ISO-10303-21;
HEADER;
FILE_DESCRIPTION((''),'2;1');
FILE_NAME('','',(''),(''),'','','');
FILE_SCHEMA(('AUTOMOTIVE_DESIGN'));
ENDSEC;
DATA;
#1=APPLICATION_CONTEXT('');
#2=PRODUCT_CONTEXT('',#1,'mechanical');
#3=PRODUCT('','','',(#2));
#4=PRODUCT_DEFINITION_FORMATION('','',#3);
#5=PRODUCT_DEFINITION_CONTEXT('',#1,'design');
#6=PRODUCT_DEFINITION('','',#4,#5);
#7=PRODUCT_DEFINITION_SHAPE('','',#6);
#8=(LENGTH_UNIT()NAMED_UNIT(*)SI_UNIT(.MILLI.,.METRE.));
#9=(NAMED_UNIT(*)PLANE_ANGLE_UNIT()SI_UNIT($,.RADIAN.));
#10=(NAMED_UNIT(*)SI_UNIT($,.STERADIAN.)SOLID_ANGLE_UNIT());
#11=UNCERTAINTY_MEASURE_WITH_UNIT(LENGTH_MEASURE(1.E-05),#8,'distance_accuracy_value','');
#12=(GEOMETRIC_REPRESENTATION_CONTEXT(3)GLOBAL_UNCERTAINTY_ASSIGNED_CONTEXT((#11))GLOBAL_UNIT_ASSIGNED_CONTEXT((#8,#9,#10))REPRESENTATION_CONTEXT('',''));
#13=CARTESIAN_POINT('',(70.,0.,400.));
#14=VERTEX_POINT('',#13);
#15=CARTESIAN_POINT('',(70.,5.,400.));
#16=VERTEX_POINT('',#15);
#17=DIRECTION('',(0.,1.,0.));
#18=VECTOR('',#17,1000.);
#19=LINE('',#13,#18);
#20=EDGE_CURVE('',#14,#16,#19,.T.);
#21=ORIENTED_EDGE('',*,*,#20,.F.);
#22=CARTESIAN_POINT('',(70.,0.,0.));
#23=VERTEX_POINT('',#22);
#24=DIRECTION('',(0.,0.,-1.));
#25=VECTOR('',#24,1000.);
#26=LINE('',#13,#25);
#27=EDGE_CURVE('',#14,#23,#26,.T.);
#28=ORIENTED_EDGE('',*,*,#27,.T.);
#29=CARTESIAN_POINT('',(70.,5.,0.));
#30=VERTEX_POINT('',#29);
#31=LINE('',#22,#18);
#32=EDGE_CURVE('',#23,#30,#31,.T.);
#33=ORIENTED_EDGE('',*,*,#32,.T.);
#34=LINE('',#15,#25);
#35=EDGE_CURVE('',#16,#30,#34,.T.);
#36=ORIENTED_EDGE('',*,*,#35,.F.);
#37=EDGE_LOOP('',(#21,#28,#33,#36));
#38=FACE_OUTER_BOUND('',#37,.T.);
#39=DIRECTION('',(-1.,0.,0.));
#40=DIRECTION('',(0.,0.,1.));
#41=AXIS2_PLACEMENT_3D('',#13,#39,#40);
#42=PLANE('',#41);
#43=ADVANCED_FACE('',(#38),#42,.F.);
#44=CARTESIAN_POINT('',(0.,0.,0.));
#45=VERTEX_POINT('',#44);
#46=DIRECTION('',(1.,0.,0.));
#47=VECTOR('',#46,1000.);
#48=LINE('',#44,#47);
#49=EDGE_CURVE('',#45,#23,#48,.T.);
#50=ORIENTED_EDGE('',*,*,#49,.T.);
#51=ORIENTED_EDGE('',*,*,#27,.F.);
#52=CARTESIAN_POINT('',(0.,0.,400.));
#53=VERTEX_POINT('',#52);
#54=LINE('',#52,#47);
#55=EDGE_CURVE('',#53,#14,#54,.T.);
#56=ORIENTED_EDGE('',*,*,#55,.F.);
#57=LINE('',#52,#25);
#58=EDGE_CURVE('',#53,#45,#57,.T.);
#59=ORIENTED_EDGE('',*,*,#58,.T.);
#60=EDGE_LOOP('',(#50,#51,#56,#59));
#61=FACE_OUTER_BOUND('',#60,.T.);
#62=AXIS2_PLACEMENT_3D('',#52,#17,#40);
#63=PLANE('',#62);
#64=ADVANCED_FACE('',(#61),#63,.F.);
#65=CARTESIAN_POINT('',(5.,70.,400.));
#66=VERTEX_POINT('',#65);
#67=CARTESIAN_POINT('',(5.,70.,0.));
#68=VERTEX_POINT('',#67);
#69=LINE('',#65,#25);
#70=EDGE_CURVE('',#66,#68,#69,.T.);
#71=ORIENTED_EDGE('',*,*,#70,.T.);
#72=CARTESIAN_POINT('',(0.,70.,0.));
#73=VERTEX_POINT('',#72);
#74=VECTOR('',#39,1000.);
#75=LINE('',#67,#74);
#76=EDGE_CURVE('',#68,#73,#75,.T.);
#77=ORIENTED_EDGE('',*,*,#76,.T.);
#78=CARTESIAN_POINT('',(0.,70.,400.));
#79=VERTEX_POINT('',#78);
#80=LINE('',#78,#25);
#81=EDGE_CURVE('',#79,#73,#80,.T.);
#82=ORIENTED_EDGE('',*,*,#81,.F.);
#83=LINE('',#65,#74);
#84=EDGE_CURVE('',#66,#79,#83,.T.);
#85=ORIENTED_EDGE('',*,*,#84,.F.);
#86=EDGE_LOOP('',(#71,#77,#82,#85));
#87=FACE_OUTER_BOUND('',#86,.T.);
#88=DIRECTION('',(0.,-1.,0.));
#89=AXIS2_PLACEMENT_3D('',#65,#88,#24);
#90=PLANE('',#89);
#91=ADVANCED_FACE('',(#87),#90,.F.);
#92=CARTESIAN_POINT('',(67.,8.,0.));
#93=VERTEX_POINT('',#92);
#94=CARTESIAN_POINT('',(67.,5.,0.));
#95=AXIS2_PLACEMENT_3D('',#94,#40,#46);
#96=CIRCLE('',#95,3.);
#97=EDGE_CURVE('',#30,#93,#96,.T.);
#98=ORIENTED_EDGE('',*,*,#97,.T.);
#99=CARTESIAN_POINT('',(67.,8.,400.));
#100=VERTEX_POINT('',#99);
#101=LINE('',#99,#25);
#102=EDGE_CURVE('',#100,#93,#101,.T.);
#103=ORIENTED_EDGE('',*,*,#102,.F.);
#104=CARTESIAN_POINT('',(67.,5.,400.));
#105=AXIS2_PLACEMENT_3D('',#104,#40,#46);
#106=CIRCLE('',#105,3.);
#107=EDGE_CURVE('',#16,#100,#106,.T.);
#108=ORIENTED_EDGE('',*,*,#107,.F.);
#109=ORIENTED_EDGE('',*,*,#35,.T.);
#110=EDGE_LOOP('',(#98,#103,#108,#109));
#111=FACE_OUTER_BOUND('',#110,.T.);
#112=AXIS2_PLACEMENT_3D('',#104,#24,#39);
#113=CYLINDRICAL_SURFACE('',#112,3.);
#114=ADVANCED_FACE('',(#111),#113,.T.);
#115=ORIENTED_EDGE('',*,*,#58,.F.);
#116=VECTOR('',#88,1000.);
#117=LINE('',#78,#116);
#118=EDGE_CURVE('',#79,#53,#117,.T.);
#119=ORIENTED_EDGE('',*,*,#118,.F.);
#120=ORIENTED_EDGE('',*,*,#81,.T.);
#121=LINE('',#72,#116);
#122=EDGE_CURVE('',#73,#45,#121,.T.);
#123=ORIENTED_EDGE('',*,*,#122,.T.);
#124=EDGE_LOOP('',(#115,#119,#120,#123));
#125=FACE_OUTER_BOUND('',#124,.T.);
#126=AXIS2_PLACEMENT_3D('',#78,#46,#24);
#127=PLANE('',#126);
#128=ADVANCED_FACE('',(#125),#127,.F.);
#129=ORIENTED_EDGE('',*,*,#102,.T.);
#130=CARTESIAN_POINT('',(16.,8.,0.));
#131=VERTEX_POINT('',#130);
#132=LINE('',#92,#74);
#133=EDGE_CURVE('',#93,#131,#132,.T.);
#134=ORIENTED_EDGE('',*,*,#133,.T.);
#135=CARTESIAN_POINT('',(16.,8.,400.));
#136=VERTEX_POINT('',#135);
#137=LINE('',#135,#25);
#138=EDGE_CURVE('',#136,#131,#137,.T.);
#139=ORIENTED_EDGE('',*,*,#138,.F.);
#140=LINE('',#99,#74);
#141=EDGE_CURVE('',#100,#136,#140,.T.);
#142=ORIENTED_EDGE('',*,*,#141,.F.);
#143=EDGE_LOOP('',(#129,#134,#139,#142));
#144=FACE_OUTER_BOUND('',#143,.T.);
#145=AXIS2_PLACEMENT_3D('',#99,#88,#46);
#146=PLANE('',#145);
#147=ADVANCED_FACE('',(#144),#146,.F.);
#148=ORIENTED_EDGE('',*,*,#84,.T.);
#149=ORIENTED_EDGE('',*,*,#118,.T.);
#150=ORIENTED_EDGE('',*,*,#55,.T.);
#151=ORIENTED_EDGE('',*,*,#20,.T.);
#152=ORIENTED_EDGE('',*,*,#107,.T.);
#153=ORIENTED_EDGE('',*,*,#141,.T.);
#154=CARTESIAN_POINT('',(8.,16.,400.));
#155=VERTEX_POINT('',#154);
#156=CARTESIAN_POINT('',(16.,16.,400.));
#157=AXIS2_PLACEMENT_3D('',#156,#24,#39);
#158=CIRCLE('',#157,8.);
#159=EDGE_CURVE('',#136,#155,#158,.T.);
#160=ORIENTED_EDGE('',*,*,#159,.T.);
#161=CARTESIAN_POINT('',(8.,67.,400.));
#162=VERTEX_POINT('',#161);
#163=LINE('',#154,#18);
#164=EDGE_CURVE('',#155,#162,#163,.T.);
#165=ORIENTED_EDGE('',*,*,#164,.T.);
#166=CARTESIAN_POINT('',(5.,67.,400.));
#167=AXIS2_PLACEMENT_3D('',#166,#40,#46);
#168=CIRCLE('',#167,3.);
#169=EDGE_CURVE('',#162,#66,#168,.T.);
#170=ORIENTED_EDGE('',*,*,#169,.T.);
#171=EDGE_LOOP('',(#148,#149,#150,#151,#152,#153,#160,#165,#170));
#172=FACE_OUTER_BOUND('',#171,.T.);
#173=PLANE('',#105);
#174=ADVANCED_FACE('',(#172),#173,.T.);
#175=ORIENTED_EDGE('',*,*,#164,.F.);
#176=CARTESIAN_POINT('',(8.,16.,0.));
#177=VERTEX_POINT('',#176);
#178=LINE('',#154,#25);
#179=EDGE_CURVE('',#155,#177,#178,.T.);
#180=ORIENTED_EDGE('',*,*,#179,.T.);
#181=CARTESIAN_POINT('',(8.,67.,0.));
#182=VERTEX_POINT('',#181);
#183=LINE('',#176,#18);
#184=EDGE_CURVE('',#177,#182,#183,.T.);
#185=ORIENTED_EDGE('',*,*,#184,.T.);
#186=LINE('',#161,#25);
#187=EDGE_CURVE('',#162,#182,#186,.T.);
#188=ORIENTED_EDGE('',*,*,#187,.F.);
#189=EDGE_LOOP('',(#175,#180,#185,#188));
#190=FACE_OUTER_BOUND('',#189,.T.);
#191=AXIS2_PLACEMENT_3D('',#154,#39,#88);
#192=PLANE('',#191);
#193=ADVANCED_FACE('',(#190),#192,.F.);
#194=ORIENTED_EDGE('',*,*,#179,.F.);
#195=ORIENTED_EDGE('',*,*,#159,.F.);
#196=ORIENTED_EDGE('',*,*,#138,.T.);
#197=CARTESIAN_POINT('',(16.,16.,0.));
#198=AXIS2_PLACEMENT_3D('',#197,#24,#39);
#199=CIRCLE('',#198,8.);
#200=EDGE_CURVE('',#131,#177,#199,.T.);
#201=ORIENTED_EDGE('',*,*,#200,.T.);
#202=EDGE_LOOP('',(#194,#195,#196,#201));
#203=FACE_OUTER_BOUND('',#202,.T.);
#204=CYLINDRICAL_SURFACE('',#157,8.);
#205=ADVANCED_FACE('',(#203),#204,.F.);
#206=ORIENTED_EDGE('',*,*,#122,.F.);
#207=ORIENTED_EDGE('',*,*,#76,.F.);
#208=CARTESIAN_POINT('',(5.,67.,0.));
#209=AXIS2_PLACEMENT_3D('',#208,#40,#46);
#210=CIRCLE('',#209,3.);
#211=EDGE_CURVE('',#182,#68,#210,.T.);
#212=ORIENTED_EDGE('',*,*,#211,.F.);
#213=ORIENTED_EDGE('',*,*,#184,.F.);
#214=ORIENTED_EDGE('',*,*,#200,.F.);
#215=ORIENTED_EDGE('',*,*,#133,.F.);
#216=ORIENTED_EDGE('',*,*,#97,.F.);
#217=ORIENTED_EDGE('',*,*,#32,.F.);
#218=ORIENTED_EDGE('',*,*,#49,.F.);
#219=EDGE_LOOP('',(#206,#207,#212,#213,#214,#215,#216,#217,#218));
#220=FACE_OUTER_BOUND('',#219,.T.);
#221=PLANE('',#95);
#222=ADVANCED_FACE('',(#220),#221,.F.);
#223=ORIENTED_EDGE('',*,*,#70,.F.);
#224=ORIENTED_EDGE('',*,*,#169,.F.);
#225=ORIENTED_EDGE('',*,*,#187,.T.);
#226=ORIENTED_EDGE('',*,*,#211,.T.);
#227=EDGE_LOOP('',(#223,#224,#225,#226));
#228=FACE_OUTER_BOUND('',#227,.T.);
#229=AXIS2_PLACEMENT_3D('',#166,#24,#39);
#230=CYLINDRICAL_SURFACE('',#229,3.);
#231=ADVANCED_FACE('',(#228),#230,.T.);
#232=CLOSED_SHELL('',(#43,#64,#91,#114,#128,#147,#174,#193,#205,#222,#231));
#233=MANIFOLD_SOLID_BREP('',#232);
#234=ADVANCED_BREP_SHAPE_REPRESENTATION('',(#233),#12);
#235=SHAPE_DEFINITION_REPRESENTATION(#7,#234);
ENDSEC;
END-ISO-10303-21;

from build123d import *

# Parameters (mm, degrees)
BOSS_EXTRUDE1_DEPTH = 400


with BuildPart() as part:
    # Sketch1 → Boss-Extrude1 (new body)
    with BuildSketch(Plane.XY):
        with BuildLine():
            Line((0, 70), (0, 0))
            Line((0, 0), (70, 0))
            Line((70, 0), (70, 5))
            ThreePointArc((70, 5), (69.121320344, 7.121320344), (67, 8))
            Line((67, 8), (16, 8))
            ThreePointArc((16, 8), (10.343145751, 10.343145751), (8, 16))
            Line((8, 16), (8, 67))
            ThreePointArc((8, 67), (7.121320344, 69.121320344), (5, 70))
            Line((5, 70), (0, 70))
        make_face()
    extrude(amount=BOSS_EXTRUDE1_DEPTH)


solid = part.part
